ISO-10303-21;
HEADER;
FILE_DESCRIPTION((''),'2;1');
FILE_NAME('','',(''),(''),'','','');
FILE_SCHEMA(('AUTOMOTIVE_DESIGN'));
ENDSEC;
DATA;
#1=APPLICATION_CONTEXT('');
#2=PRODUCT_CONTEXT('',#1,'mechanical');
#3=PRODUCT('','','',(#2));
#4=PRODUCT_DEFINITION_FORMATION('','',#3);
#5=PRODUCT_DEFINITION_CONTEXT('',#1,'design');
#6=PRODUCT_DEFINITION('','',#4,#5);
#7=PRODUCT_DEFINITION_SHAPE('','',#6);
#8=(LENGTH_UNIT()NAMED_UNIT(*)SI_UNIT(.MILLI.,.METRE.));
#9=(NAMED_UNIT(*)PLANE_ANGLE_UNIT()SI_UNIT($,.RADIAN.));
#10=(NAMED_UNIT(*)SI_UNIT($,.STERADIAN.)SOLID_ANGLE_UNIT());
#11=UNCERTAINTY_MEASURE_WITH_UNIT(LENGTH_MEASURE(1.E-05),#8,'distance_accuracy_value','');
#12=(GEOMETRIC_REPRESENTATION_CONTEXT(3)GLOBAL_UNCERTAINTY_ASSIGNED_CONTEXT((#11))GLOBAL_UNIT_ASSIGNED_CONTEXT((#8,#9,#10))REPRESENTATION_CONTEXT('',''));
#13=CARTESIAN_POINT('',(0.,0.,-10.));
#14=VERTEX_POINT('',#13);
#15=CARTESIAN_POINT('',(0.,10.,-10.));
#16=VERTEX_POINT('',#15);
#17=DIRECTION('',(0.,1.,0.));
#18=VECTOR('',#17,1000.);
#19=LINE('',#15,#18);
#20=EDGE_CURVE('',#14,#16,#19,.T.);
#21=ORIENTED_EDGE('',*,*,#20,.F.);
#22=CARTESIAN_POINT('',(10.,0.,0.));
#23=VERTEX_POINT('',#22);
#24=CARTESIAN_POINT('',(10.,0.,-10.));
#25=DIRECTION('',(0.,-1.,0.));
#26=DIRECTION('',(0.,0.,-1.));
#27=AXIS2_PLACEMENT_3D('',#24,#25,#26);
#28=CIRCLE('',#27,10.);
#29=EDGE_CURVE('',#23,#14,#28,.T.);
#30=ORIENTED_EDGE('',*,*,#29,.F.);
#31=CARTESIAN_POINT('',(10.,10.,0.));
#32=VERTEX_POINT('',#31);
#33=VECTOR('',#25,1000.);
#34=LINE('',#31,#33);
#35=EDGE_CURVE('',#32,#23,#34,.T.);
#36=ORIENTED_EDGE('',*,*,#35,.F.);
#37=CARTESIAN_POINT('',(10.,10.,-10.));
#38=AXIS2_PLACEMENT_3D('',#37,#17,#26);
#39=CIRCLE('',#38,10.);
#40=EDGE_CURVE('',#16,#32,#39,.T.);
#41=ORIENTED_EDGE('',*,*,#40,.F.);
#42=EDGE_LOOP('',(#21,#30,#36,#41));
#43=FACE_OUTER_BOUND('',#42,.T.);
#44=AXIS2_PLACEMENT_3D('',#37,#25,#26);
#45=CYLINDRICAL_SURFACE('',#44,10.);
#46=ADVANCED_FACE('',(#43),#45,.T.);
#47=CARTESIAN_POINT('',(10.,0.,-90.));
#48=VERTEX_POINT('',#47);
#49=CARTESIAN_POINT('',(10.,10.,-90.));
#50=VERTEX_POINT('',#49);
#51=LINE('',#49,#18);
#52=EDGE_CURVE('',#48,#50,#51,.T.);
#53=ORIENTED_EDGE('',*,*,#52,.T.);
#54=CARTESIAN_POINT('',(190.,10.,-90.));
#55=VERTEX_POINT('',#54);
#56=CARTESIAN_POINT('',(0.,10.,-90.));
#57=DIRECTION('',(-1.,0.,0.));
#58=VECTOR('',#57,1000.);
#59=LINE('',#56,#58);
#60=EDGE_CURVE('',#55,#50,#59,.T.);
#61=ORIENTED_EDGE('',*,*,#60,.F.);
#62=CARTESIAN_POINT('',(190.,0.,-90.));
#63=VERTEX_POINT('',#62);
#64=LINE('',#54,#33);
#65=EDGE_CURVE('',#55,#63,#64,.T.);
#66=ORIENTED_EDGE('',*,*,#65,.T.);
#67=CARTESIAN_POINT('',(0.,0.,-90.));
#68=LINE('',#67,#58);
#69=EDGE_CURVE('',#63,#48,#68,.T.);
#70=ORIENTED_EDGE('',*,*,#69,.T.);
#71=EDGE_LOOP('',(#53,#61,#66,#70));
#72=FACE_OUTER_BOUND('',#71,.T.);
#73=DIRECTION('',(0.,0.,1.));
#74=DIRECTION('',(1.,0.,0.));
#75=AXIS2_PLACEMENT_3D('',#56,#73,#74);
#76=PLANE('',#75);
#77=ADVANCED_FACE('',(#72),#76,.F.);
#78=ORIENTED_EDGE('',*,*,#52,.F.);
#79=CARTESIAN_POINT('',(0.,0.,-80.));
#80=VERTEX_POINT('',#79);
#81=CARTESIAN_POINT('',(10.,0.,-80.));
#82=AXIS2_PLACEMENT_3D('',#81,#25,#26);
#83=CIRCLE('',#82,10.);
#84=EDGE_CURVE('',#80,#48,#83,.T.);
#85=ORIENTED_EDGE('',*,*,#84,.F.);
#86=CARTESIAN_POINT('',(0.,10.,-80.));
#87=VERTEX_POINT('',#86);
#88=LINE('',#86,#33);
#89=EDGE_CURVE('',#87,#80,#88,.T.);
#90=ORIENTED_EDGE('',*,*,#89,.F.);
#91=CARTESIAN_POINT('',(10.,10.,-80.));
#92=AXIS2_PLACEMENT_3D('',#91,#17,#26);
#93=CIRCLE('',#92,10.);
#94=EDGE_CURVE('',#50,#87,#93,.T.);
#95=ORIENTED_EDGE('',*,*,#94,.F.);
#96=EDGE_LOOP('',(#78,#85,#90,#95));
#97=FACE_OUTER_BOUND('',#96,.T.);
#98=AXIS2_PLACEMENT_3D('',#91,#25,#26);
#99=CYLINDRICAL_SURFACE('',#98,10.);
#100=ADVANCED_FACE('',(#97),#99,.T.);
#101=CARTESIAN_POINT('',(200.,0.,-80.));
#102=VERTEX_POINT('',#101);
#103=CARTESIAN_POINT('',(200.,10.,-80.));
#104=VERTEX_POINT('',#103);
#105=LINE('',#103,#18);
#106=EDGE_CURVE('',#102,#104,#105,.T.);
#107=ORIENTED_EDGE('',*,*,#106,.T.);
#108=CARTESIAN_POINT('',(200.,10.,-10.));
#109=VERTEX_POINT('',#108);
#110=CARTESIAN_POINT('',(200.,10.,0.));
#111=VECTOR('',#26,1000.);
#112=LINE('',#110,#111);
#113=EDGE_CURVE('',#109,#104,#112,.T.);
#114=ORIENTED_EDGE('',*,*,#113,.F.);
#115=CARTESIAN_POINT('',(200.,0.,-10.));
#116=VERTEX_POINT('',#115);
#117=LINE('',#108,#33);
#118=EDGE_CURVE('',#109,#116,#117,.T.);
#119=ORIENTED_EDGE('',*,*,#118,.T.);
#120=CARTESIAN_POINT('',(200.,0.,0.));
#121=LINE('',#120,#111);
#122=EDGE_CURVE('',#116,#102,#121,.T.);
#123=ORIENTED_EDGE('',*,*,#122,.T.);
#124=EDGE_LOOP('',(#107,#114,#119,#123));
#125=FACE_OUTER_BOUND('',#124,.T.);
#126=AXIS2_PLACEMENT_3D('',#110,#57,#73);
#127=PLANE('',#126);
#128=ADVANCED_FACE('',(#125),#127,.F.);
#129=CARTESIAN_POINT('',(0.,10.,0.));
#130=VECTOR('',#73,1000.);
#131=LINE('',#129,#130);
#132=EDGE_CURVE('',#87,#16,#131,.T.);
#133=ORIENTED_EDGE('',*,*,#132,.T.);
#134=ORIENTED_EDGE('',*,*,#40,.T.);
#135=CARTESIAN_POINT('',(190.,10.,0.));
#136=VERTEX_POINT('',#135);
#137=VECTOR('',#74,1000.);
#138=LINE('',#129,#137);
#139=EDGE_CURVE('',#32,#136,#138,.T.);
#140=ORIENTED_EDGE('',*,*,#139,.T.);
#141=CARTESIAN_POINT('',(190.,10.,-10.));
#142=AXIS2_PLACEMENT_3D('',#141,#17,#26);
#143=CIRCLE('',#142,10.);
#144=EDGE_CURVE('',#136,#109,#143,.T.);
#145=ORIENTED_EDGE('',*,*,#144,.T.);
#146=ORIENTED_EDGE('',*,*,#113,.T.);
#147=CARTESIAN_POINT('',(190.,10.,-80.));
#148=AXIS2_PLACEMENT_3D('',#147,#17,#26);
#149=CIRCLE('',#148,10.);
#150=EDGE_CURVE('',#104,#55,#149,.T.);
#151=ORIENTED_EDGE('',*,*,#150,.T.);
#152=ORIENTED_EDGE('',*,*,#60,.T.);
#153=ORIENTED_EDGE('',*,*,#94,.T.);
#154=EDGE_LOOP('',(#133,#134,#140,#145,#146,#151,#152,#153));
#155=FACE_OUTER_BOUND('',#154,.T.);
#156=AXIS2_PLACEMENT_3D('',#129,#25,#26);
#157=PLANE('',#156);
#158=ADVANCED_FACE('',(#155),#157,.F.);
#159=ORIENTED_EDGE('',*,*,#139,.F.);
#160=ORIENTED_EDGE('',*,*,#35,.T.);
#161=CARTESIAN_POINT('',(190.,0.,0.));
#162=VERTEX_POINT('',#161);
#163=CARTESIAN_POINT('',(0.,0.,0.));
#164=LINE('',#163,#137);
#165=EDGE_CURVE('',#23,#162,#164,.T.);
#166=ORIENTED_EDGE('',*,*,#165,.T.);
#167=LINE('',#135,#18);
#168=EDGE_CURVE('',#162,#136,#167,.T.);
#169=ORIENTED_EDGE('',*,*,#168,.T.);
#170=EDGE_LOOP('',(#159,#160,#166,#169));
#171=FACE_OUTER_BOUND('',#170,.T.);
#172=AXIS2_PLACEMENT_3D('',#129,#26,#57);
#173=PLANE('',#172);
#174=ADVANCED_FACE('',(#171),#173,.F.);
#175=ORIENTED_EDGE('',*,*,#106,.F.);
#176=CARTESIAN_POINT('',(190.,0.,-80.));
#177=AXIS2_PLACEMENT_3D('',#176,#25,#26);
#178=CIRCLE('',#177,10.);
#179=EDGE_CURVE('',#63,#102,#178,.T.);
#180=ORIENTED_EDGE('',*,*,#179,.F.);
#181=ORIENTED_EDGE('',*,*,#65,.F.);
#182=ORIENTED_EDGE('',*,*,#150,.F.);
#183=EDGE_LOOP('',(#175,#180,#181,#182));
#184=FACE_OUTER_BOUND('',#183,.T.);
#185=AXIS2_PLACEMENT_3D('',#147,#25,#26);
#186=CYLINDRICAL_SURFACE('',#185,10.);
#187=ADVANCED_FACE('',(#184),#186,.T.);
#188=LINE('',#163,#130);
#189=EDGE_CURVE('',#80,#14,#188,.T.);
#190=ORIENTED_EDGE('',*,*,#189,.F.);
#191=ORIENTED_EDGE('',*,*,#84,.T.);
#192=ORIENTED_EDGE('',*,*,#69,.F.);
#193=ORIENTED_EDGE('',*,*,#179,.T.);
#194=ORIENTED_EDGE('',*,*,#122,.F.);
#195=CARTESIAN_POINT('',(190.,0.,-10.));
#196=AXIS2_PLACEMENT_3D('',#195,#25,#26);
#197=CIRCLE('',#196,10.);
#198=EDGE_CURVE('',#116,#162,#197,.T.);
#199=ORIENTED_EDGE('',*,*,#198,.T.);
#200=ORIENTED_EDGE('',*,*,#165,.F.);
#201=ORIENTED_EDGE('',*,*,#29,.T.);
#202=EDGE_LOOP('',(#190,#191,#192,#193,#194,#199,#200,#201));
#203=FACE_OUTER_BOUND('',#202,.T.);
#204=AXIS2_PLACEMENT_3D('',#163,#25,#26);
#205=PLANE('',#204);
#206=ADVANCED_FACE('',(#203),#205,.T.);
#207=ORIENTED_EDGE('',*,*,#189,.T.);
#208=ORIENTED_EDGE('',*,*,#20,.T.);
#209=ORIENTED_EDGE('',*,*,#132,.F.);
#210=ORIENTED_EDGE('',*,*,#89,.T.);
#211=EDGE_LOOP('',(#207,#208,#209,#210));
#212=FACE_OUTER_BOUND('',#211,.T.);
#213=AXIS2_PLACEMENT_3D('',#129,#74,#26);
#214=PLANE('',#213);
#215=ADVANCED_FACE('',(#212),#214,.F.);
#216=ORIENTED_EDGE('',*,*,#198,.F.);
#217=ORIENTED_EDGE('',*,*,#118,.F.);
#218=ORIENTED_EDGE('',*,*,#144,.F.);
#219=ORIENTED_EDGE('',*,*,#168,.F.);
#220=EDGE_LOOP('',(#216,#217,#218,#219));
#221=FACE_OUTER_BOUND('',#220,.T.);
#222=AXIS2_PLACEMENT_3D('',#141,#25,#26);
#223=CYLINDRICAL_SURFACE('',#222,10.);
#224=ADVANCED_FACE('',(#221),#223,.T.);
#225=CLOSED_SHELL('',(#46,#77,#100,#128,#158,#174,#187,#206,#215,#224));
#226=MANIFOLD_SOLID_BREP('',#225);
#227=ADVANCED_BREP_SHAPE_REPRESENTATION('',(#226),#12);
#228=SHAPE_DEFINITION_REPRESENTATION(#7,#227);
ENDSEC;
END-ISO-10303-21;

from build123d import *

# Parameters (mm, degrees)
SKETCH1_W           = 200
SKETCH1_H           = 90
BOSS_EXTRUDE1_DEPTH = 10
FILLET1_R           = 10


with BuildPart() as part:
    # Sketch1 → Boss-Extrude1 (new body)
    with BuildSketch(Plane(origin=(0, 0, 0), x_dir=(1, 0, 0), z_dir=(0, 1, 0))):
        with Locations((100, 45)):
            Rectangle(SKETCH1_W, SKETCH1_H)
    extrude(amount=BOSS_EXTRUDE1_DEPTH)

    # Fillet1
    fillet1_edges = [part.edges().sort_by_distance(p)[0] for p in [
        (0, 5, -90),
        (200, 5, -90),
        (200, 5, 0),
        (0, 5, 0),
    ]]
    fillet(fillet1_edges, radius=FILLET1_R)


solid = part.part
